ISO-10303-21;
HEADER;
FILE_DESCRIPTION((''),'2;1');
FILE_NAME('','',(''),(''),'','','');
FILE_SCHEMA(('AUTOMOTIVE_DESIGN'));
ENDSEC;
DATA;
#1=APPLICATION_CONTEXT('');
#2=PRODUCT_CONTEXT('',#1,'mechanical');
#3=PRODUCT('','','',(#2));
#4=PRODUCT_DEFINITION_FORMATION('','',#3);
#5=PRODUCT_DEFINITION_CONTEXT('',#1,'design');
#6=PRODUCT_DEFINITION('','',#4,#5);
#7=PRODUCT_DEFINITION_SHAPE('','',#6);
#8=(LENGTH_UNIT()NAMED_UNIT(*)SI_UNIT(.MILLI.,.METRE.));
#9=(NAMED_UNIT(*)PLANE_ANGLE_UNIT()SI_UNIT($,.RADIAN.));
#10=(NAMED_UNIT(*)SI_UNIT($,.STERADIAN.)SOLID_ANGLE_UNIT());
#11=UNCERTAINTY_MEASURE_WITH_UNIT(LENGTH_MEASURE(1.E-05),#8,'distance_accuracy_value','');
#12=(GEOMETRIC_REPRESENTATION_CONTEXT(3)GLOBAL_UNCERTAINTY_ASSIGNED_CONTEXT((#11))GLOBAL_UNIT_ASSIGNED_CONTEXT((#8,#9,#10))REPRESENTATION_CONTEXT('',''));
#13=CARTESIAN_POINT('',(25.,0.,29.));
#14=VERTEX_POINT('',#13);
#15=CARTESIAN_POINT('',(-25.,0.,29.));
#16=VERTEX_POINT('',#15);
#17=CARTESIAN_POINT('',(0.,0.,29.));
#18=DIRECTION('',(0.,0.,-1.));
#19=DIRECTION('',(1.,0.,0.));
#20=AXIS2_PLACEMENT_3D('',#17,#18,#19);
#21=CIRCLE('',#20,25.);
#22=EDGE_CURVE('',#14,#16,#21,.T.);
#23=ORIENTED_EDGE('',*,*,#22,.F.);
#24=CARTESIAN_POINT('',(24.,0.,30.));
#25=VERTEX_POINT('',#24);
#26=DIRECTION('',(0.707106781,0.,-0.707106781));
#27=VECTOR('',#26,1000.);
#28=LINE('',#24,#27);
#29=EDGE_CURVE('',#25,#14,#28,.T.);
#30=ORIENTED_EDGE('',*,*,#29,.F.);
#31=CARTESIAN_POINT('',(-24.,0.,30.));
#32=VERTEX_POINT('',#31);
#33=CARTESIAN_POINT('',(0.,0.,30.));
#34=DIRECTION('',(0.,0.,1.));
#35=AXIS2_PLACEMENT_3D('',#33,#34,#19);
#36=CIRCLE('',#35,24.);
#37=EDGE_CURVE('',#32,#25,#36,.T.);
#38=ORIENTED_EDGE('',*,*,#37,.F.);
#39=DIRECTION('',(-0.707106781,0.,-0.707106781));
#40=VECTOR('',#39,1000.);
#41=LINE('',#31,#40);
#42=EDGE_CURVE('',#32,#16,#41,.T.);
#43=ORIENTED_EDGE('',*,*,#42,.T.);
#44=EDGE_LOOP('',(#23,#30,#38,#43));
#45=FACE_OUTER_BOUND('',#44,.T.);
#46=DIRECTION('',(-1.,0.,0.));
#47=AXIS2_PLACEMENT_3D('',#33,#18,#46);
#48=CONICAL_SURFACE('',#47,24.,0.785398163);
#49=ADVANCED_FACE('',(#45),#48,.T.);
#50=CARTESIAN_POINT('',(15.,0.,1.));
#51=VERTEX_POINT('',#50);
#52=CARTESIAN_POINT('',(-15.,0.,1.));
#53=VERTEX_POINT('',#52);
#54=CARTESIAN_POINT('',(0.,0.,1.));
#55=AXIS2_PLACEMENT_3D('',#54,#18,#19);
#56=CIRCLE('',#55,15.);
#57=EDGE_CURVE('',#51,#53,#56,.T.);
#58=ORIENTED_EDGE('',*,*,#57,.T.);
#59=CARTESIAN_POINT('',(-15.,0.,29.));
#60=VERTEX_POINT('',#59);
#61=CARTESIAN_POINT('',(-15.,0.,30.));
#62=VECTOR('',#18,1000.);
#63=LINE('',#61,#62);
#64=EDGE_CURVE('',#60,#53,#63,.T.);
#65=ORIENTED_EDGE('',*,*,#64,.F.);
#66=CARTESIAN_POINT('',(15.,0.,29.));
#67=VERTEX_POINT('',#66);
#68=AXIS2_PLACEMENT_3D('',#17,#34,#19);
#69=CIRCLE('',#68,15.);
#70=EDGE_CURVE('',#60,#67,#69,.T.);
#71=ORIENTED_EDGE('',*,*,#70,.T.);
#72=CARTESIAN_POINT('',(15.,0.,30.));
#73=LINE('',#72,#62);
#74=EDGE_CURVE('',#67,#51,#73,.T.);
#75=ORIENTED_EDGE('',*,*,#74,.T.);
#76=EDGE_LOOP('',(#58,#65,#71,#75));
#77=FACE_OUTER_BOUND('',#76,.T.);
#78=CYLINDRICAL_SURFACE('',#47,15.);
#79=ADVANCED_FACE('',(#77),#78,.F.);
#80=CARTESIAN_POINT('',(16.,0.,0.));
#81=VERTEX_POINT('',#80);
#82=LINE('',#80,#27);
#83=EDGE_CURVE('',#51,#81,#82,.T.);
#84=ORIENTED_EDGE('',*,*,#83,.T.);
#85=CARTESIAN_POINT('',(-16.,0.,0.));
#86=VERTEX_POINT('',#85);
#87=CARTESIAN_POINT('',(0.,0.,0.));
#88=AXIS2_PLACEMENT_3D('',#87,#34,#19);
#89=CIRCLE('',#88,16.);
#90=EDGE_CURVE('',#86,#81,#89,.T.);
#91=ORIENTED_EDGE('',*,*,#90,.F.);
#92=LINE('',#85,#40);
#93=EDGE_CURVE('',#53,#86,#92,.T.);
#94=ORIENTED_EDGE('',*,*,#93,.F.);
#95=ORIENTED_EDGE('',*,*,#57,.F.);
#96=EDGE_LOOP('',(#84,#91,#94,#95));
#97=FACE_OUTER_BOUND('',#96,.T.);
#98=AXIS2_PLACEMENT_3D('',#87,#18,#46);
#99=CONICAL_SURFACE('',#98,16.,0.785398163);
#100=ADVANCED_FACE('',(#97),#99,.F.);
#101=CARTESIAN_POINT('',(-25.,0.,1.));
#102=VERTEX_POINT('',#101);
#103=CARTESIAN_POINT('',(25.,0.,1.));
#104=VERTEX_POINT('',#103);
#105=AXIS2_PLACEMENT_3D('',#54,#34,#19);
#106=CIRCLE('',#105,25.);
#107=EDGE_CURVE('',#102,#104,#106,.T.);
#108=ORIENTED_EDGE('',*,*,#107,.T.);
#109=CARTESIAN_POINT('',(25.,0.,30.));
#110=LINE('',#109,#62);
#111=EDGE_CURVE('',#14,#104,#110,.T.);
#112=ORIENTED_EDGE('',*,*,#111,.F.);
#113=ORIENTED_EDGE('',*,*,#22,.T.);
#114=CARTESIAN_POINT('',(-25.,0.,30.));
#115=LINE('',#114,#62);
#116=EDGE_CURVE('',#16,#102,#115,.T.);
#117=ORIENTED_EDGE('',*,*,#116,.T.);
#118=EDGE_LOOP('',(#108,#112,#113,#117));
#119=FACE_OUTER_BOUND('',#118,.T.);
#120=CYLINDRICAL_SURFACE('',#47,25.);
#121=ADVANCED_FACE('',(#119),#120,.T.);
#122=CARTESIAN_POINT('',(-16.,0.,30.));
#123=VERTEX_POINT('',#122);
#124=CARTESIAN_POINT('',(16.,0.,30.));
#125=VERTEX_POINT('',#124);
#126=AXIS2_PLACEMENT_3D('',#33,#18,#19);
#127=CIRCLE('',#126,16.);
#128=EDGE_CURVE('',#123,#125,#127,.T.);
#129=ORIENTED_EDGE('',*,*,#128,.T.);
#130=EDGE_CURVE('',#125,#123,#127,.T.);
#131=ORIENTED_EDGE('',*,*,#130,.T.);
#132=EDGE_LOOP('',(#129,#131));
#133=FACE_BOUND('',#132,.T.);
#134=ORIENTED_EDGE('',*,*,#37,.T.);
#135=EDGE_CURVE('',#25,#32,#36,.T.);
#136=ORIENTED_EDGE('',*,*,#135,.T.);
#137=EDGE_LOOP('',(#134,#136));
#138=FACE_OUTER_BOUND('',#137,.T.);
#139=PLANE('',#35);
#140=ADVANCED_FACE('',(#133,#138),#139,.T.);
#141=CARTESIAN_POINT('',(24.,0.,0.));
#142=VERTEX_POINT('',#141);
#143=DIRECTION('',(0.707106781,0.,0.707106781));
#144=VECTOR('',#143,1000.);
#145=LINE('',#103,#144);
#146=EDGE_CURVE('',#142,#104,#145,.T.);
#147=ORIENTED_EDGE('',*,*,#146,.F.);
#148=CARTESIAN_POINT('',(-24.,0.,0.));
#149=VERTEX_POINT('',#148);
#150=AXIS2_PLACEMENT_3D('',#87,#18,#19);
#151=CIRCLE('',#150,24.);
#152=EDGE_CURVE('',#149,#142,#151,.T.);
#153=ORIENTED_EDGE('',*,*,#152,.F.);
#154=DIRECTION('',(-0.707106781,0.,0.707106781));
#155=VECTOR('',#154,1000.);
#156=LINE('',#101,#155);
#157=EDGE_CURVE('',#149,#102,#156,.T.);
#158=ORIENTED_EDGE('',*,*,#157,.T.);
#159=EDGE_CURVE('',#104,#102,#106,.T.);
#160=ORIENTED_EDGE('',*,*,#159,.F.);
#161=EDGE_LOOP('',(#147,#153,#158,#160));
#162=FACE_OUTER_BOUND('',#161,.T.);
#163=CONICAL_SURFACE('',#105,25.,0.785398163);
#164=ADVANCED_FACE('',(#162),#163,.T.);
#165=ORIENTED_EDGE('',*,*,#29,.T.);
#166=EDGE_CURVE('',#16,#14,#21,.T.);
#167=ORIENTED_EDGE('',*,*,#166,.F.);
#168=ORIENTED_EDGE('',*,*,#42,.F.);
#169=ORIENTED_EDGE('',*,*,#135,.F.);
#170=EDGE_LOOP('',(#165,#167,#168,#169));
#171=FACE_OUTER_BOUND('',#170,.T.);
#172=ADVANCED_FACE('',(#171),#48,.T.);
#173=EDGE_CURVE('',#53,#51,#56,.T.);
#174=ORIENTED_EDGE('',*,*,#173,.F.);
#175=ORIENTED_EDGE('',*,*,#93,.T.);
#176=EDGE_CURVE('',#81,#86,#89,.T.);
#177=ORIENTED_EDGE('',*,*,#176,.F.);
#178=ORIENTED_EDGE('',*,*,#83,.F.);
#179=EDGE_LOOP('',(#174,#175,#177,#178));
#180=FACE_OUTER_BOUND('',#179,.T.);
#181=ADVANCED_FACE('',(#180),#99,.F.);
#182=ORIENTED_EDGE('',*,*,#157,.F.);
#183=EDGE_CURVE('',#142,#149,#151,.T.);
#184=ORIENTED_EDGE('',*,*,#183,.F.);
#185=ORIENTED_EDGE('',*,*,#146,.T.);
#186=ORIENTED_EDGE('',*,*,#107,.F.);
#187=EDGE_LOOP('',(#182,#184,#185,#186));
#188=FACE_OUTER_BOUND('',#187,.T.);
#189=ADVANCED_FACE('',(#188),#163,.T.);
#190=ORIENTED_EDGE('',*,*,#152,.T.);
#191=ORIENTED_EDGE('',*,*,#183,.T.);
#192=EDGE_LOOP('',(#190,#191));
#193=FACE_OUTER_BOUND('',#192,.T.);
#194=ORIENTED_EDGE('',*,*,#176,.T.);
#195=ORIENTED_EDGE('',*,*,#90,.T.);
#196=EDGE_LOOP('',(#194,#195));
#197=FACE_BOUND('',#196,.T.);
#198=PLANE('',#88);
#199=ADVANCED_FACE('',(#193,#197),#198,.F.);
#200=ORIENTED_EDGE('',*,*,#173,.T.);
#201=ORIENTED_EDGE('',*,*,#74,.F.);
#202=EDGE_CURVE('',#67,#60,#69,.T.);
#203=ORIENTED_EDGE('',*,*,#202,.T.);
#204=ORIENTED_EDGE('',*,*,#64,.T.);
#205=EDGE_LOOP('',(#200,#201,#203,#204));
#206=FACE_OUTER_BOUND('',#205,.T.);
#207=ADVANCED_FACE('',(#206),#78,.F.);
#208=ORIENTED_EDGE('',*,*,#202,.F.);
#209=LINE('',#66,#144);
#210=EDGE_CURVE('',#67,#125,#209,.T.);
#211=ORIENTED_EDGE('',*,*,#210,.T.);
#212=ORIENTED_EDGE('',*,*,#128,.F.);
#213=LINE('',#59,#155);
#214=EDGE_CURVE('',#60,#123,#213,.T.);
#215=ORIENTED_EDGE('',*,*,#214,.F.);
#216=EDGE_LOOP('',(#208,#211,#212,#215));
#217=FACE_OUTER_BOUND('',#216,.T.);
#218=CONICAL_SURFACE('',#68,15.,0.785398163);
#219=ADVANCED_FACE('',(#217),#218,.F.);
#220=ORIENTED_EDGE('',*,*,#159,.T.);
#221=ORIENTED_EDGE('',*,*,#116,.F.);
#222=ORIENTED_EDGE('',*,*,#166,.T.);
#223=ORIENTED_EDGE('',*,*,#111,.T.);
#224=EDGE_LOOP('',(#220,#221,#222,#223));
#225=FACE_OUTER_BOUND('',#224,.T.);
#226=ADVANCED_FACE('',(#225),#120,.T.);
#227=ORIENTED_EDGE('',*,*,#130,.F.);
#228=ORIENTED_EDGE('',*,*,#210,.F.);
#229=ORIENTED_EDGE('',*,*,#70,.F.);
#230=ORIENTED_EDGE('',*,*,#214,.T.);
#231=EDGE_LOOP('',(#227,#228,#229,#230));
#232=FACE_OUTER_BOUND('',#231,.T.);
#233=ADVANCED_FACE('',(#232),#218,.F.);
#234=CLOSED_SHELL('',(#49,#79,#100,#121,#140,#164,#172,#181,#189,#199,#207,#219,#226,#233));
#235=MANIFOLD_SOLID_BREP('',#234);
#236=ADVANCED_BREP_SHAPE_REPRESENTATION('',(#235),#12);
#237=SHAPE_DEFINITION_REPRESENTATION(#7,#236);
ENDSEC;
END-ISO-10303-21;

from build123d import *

# Parameters (mm, degrees)
SKETCH1_R           = 25
SKETCH1_R_2         = 15
BOSS_EXTRUDE1_DEPTH = 30
CHAMFER1_SIZE       = 1


with BuildPart() as part:
    # Sketch1 → Boss-Extrude1 (new body)
    with BuildSketch(Plane.XY):
        Circle(SKETCH1_R)
        Circle(SKETCH1_R_2, mode=Mode.SUBTRACT)
    extrude(amount=BOSS_EXTRUDE1_DEPTH)

    # Chamfer1
    chamfer1_edges = [part.edges().sort_by_distance(p)[0] for p in [
        (-25, 0, 0),
        (-25, 0, 30),
        (-15, 0, 0),
        (-15, 0, 30),
    ]]
    chamfer(chamfer1_edges, length=CHAMFER1_SIZE)


solid = part.part
